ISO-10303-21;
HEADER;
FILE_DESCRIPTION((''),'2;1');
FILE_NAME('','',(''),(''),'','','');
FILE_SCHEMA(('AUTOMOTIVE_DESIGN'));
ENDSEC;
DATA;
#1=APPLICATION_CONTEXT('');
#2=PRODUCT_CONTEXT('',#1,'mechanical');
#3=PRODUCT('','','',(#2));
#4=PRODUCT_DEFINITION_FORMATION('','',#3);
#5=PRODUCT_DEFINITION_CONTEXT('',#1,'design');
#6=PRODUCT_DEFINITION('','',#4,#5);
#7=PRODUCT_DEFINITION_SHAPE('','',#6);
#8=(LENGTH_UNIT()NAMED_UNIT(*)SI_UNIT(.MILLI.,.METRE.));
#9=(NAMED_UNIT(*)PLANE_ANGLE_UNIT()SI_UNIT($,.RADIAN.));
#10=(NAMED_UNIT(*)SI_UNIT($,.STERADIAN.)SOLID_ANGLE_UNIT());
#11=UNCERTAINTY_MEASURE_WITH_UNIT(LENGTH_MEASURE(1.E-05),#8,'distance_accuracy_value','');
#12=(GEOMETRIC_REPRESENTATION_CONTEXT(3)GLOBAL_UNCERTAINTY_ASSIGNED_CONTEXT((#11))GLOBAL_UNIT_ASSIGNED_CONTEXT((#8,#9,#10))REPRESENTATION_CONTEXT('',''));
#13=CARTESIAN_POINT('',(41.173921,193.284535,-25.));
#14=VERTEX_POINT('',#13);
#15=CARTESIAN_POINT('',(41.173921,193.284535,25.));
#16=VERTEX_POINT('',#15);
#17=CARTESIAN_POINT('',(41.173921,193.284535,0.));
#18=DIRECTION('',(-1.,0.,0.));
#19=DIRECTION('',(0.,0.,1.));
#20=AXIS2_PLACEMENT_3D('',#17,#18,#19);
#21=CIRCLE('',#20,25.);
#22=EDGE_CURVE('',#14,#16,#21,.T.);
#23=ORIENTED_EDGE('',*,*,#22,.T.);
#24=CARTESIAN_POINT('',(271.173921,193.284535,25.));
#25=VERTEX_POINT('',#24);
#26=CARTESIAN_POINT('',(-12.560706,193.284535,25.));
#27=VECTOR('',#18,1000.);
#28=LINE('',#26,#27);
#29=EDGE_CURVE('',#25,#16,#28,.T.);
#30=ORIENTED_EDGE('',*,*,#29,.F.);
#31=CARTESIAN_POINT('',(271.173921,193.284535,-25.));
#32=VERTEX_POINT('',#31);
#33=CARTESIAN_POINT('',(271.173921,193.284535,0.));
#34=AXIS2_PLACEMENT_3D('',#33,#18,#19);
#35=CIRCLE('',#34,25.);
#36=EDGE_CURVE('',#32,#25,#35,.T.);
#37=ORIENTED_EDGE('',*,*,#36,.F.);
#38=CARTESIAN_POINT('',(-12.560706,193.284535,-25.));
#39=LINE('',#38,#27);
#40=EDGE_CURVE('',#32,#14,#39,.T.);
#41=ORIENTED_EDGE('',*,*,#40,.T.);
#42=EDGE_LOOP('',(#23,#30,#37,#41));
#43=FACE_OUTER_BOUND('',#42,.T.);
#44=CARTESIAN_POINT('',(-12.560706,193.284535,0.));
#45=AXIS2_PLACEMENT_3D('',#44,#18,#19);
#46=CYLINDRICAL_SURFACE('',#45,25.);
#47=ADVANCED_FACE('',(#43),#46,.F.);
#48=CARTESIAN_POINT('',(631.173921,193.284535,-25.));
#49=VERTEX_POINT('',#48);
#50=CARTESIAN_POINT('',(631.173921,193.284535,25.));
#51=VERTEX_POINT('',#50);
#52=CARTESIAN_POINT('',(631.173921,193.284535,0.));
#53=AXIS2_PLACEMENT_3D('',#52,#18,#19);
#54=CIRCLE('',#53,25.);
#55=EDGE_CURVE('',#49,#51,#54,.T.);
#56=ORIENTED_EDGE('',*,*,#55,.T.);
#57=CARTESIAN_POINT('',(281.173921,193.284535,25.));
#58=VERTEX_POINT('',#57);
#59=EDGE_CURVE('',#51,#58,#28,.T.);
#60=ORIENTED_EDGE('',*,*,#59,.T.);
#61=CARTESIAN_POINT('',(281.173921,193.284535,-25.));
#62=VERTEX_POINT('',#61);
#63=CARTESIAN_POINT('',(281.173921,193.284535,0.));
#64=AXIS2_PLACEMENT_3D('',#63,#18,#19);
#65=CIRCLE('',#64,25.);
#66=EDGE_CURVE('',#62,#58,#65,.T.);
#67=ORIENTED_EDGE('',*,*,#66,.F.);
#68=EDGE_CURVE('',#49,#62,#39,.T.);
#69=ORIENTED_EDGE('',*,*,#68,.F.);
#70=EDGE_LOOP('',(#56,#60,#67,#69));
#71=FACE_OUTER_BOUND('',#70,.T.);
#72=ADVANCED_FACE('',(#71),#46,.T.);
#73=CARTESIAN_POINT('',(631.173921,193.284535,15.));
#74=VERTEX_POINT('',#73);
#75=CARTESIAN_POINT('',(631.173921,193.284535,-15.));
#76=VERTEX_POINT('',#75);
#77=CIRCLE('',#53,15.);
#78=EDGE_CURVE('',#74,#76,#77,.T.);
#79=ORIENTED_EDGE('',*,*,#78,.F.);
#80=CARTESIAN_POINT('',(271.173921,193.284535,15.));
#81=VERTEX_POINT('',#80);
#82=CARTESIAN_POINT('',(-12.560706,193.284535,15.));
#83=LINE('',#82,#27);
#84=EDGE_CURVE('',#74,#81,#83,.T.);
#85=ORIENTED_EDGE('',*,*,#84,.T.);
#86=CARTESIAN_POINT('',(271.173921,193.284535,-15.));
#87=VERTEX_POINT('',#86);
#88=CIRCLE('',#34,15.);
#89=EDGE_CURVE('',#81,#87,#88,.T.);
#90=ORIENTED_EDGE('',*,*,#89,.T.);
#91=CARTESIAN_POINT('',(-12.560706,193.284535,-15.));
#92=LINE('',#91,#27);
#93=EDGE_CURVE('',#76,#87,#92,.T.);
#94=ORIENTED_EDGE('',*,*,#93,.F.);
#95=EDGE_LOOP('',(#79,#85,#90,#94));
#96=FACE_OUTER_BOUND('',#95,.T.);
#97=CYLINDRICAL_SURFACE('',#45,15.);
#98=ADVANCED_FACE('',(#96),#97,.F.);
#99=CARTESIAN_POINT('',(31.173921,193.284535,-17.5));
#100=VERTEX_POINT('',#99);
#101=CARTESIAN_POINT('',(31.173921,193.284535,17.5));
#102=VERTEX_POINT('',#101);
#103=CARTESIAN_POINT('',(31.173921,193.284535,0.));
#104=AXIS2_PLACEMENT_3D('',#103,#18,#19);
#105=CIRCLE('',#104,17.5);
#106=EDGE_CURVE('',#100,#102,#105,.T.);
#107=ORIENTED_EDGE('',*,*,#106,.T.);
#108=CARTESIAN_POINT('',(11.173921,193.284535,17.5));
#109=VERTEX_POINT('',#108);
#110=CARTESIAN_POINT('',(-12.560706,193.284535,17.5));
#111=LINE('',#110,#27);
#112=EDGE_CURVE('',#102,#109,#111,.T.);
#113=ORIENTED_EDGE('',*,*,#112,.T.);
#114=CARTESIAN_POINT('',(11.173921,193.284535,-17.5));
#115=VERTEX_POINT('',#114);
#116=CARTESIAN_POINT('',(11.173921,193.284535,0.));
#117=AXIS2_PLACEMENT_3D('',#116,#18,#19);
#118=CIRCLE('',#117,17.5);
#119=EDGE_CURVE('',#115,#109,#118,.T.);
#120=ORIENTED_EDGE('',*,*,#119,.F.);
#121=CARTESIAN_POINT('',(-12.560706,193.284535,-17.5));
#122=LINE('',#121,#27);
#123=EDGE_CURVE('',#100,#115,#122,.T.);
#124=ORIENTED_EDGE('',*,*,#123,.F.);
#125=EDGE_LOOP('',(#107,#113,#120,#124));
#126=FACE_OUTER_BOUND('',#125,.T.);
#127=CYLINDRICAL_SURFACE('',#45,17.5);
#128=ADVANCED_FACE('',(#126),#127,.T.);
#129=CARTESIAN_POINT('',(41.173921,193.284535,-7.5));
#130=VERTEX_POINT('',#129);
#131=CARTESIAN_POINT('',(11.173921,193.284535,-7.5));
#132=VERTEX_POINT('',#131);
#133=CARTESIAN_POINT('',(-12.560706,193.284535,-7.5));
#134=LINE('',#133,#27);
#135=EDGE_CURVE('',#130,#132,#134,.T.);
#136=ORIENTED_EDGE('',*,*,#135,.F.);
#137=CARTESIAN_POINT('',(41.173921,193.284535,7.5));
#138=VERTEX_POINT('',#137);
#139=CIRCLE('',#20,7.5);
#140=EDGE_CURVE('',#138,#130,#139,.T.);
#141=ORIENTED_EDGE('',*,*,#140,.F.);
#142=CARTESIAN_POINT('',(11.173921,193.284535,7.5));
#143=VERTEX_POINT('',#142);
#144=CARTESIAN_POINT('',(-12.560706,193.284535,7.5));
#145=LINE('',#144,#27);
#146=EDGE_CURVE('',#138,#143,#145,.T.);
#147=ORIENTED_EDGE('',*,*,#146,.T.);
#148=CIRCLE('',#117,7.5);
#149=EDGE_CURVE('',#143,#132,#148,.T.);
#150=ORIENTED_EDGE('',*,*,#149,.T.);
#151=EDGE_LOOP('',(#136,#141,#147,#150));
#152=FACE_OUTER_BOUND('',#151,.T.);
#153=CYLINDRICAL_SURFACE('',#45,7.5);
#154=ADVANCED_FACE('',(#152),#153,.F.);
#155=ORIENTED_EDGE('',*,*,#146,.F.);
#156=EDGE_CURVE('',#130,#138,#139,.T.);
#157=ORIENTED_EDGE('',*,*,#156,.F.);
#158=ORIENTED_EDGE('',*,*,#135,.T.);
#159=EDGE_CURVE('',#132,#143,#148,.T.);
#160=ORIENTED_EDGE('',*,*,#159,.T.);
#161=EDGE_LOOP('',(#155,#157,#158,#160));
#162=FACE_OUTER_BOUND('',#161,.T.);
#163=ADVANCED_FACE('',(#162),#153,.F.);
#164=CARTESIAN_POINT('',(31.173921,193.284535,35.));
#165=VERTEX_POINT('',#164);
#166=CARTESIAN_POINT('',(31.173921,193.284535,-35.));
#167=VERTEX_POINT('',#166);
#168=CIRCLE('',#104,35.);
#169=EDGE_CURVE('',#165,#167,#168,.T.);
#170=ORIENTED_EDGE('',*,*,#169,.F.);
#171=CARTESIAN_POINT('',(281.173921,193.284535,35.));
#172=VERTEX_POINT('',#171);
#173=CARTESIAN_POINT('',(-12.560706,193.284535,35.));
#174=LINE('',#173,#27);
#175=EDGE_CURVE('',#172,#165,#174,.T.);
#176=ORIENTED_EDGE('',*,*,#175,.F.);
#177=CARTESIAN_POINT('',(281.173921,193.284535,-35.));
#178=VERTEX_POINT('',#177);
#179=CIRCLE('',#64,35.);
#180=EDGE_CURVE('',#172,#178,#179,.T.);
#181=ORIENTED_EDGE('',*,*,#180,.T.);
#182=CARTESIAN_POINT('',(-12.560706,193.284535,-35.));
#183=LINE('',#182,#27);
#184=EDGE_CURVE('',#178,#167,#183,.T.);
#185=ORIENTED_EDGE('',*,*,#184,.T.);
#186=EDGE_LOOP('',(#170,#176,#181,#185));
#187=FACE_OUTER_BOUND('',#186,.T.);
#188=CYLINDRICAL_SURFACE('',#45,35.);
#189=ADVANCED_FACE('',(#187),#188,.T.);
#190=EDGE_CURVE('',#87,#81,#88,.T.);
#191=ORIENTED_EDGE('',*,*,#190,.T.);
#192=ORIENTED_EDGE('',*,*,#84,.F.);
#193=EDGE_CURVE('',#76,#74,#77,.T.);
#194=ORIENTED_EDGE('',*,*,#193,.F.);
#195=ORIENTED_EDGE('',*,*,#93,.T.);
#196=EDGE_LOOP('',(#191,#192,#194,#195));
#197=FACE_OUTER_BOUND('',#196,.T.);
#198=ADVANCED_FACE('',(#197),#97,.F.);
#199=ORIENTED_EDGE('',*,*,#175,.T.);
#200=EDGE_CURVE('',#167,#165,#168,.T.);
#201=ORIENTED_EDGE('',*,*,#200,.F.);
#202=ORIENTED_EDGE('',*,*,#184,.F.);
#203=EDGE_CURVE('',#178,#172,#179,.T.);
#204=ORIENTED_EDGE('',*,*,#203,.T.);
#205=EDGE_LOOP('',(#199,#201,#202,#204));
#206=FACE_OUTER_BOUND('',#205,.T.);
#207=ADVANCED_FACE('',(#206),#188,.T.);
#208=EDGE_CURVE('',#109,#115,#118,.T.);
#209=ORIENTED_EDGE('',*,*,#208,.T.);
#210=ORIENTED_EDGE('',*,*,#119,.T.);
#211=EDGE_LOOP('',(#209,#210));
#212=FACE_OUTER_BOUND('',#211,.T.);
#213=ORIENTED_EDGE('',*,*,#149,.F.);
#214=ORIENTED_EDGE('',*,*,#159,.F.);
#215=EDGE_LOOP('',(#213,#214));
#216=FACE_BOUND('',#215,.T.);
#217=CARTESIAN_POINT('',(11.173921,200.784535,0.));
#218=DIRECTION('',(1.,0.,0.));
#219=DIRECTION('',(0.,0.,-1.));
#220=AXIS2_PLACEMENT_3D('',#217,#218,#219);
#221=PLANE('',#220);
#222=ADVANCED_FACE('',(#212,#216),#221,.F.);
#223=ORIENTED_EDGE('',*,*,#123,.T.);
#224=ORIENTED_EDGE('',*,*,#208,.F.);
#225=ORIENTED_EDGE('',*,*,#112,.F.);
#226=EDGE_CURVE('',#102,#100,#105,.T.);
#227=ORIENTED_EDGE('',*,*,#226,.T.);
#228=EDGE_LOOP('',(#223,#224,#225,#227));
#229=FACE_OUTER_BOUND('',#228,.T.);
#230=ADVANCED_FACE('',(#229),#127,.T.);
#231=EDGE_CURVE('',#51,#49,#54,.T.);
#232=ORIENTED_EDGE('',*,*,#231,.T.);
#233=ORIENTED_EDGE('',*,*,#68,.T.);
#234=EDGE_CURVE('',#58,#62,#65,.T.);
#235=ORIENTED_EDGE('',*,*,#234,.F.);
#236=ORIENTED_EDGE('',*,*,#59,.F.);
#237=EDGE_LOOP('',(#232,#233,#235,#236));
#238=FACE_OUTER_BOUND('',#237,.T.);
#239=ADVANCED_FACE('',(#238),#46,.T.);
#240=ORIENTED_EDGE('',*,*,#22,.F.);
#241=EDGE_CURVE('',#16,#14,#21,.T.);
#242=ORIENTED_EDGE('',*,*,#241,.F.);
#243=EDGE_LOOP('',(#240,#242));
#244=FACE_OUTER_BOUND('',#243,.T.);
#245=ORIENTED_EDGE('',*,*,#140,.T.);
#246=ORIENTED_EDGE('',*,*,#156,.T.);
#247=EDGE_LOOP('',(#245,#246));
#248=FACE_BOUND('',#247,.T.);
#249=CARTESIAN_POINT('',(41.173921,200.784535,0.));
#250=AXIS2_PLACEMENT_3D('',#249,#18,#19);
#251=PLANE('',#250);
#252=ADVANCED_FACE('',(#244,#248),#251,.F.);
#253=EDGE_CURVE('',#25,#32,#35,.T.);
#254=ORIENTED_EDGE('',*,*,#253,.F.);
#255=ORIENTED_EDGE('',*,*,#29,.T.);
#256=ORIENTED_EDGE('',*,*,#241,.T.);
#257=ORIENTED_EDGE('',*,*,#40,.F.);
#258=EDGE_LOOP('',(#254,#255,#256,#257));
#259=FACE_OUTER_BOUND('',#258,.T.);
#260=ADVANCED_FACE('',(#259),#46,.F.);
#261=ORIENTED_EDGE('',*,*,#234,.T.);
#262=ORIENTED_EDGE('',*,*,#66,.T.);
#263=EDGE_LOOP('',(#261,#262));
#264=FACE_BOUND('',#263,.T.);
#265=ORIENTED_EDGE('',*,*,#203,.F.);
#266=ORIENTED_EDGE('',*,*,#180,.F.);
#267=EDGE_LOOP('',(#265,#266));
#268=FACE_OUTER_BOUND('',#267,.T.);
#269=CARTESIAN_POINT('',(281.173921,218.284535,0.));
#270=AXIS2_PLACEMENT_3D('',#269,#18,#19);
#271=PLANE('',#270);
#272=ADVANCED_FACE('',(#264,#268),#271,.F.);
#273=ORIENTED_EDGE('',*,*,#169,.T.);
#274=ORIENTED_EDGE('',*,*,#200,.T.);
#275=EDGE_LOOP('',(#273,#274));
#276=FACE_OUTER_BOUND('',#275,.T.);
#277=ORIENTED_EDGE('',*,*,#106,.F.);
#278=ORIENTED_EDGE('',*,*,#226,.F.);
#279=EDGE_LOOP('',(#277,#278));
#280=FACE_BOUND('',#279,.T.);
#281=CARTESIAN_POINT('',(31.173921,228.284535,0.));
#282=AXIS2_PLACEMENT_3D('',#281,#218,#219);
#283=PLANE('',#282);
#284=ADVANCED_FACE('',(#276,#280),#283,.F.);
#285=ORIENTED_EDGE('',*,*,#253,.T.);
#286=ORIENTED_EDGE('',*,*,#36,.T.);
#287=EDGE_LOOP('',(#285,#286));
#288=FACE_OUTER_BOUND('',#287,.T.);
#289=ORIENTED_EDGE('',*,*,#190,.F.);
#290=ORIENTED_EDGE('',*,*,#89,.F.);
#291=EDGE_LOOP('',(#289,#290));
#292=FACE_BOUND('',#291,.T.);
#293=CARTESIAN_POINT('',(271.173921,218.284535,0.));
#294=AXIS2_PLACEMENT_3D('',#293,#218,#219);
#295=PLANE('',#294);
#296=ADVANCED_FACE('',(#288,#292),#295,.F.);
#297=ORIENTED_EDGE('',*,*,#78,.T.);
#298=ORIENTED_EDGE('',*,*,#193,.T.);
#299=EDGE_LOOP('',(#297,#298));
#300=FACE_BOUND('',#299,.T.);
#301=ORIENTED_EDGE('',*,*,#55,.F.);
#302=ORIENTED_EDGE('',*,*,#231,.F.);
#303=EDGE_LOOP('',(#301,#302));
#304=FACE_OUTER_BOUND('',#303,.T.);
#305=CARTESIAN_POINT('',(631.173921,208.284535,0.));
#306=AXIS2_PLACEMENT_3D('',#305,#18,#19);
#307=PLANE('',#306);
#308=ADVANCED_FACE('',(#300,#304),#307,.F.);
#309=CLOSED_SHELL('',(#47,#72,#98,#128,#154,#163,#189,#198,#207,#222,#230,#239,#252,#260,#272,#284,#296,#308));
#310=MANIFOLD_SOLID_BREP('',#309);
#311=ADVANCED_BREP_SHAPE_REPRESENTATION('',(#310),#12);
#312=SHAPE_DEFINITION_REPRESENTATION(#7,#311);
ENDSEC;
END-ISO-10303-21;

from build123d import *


with BuildPart() as part:
    # Sketch1 → Revolve1 (revolve)
    with BuildSketch(Plane.XY, mode=Mode.PRIVATE) as revolve1_sk:
        Polygon((631.173921275, 208.284534899), (631.173921275, 218.284534899), (281.173921275, 218.284534899), (281.173921275, 228.284534899), (31.173921275, 228.284534899), (31.173921275, 210.784534899), (11.173921275, 210.784534899), (11.173921275, 200.784534899), (41.173921275, 200.784534899), (41.173921275, 218.284534899), (271.173921275, 218.284534899), (271.173921275, 208.284534899), align=None)
    revolve(revolve1_sk.sketch.rotate(Axis((-12.5607058, 193.284534899, 0), (1, 0, 0)), 90), axis=Axis((-12.5607058, 193.284534899, 0), (1, 0, 0)))


solid = part.part
